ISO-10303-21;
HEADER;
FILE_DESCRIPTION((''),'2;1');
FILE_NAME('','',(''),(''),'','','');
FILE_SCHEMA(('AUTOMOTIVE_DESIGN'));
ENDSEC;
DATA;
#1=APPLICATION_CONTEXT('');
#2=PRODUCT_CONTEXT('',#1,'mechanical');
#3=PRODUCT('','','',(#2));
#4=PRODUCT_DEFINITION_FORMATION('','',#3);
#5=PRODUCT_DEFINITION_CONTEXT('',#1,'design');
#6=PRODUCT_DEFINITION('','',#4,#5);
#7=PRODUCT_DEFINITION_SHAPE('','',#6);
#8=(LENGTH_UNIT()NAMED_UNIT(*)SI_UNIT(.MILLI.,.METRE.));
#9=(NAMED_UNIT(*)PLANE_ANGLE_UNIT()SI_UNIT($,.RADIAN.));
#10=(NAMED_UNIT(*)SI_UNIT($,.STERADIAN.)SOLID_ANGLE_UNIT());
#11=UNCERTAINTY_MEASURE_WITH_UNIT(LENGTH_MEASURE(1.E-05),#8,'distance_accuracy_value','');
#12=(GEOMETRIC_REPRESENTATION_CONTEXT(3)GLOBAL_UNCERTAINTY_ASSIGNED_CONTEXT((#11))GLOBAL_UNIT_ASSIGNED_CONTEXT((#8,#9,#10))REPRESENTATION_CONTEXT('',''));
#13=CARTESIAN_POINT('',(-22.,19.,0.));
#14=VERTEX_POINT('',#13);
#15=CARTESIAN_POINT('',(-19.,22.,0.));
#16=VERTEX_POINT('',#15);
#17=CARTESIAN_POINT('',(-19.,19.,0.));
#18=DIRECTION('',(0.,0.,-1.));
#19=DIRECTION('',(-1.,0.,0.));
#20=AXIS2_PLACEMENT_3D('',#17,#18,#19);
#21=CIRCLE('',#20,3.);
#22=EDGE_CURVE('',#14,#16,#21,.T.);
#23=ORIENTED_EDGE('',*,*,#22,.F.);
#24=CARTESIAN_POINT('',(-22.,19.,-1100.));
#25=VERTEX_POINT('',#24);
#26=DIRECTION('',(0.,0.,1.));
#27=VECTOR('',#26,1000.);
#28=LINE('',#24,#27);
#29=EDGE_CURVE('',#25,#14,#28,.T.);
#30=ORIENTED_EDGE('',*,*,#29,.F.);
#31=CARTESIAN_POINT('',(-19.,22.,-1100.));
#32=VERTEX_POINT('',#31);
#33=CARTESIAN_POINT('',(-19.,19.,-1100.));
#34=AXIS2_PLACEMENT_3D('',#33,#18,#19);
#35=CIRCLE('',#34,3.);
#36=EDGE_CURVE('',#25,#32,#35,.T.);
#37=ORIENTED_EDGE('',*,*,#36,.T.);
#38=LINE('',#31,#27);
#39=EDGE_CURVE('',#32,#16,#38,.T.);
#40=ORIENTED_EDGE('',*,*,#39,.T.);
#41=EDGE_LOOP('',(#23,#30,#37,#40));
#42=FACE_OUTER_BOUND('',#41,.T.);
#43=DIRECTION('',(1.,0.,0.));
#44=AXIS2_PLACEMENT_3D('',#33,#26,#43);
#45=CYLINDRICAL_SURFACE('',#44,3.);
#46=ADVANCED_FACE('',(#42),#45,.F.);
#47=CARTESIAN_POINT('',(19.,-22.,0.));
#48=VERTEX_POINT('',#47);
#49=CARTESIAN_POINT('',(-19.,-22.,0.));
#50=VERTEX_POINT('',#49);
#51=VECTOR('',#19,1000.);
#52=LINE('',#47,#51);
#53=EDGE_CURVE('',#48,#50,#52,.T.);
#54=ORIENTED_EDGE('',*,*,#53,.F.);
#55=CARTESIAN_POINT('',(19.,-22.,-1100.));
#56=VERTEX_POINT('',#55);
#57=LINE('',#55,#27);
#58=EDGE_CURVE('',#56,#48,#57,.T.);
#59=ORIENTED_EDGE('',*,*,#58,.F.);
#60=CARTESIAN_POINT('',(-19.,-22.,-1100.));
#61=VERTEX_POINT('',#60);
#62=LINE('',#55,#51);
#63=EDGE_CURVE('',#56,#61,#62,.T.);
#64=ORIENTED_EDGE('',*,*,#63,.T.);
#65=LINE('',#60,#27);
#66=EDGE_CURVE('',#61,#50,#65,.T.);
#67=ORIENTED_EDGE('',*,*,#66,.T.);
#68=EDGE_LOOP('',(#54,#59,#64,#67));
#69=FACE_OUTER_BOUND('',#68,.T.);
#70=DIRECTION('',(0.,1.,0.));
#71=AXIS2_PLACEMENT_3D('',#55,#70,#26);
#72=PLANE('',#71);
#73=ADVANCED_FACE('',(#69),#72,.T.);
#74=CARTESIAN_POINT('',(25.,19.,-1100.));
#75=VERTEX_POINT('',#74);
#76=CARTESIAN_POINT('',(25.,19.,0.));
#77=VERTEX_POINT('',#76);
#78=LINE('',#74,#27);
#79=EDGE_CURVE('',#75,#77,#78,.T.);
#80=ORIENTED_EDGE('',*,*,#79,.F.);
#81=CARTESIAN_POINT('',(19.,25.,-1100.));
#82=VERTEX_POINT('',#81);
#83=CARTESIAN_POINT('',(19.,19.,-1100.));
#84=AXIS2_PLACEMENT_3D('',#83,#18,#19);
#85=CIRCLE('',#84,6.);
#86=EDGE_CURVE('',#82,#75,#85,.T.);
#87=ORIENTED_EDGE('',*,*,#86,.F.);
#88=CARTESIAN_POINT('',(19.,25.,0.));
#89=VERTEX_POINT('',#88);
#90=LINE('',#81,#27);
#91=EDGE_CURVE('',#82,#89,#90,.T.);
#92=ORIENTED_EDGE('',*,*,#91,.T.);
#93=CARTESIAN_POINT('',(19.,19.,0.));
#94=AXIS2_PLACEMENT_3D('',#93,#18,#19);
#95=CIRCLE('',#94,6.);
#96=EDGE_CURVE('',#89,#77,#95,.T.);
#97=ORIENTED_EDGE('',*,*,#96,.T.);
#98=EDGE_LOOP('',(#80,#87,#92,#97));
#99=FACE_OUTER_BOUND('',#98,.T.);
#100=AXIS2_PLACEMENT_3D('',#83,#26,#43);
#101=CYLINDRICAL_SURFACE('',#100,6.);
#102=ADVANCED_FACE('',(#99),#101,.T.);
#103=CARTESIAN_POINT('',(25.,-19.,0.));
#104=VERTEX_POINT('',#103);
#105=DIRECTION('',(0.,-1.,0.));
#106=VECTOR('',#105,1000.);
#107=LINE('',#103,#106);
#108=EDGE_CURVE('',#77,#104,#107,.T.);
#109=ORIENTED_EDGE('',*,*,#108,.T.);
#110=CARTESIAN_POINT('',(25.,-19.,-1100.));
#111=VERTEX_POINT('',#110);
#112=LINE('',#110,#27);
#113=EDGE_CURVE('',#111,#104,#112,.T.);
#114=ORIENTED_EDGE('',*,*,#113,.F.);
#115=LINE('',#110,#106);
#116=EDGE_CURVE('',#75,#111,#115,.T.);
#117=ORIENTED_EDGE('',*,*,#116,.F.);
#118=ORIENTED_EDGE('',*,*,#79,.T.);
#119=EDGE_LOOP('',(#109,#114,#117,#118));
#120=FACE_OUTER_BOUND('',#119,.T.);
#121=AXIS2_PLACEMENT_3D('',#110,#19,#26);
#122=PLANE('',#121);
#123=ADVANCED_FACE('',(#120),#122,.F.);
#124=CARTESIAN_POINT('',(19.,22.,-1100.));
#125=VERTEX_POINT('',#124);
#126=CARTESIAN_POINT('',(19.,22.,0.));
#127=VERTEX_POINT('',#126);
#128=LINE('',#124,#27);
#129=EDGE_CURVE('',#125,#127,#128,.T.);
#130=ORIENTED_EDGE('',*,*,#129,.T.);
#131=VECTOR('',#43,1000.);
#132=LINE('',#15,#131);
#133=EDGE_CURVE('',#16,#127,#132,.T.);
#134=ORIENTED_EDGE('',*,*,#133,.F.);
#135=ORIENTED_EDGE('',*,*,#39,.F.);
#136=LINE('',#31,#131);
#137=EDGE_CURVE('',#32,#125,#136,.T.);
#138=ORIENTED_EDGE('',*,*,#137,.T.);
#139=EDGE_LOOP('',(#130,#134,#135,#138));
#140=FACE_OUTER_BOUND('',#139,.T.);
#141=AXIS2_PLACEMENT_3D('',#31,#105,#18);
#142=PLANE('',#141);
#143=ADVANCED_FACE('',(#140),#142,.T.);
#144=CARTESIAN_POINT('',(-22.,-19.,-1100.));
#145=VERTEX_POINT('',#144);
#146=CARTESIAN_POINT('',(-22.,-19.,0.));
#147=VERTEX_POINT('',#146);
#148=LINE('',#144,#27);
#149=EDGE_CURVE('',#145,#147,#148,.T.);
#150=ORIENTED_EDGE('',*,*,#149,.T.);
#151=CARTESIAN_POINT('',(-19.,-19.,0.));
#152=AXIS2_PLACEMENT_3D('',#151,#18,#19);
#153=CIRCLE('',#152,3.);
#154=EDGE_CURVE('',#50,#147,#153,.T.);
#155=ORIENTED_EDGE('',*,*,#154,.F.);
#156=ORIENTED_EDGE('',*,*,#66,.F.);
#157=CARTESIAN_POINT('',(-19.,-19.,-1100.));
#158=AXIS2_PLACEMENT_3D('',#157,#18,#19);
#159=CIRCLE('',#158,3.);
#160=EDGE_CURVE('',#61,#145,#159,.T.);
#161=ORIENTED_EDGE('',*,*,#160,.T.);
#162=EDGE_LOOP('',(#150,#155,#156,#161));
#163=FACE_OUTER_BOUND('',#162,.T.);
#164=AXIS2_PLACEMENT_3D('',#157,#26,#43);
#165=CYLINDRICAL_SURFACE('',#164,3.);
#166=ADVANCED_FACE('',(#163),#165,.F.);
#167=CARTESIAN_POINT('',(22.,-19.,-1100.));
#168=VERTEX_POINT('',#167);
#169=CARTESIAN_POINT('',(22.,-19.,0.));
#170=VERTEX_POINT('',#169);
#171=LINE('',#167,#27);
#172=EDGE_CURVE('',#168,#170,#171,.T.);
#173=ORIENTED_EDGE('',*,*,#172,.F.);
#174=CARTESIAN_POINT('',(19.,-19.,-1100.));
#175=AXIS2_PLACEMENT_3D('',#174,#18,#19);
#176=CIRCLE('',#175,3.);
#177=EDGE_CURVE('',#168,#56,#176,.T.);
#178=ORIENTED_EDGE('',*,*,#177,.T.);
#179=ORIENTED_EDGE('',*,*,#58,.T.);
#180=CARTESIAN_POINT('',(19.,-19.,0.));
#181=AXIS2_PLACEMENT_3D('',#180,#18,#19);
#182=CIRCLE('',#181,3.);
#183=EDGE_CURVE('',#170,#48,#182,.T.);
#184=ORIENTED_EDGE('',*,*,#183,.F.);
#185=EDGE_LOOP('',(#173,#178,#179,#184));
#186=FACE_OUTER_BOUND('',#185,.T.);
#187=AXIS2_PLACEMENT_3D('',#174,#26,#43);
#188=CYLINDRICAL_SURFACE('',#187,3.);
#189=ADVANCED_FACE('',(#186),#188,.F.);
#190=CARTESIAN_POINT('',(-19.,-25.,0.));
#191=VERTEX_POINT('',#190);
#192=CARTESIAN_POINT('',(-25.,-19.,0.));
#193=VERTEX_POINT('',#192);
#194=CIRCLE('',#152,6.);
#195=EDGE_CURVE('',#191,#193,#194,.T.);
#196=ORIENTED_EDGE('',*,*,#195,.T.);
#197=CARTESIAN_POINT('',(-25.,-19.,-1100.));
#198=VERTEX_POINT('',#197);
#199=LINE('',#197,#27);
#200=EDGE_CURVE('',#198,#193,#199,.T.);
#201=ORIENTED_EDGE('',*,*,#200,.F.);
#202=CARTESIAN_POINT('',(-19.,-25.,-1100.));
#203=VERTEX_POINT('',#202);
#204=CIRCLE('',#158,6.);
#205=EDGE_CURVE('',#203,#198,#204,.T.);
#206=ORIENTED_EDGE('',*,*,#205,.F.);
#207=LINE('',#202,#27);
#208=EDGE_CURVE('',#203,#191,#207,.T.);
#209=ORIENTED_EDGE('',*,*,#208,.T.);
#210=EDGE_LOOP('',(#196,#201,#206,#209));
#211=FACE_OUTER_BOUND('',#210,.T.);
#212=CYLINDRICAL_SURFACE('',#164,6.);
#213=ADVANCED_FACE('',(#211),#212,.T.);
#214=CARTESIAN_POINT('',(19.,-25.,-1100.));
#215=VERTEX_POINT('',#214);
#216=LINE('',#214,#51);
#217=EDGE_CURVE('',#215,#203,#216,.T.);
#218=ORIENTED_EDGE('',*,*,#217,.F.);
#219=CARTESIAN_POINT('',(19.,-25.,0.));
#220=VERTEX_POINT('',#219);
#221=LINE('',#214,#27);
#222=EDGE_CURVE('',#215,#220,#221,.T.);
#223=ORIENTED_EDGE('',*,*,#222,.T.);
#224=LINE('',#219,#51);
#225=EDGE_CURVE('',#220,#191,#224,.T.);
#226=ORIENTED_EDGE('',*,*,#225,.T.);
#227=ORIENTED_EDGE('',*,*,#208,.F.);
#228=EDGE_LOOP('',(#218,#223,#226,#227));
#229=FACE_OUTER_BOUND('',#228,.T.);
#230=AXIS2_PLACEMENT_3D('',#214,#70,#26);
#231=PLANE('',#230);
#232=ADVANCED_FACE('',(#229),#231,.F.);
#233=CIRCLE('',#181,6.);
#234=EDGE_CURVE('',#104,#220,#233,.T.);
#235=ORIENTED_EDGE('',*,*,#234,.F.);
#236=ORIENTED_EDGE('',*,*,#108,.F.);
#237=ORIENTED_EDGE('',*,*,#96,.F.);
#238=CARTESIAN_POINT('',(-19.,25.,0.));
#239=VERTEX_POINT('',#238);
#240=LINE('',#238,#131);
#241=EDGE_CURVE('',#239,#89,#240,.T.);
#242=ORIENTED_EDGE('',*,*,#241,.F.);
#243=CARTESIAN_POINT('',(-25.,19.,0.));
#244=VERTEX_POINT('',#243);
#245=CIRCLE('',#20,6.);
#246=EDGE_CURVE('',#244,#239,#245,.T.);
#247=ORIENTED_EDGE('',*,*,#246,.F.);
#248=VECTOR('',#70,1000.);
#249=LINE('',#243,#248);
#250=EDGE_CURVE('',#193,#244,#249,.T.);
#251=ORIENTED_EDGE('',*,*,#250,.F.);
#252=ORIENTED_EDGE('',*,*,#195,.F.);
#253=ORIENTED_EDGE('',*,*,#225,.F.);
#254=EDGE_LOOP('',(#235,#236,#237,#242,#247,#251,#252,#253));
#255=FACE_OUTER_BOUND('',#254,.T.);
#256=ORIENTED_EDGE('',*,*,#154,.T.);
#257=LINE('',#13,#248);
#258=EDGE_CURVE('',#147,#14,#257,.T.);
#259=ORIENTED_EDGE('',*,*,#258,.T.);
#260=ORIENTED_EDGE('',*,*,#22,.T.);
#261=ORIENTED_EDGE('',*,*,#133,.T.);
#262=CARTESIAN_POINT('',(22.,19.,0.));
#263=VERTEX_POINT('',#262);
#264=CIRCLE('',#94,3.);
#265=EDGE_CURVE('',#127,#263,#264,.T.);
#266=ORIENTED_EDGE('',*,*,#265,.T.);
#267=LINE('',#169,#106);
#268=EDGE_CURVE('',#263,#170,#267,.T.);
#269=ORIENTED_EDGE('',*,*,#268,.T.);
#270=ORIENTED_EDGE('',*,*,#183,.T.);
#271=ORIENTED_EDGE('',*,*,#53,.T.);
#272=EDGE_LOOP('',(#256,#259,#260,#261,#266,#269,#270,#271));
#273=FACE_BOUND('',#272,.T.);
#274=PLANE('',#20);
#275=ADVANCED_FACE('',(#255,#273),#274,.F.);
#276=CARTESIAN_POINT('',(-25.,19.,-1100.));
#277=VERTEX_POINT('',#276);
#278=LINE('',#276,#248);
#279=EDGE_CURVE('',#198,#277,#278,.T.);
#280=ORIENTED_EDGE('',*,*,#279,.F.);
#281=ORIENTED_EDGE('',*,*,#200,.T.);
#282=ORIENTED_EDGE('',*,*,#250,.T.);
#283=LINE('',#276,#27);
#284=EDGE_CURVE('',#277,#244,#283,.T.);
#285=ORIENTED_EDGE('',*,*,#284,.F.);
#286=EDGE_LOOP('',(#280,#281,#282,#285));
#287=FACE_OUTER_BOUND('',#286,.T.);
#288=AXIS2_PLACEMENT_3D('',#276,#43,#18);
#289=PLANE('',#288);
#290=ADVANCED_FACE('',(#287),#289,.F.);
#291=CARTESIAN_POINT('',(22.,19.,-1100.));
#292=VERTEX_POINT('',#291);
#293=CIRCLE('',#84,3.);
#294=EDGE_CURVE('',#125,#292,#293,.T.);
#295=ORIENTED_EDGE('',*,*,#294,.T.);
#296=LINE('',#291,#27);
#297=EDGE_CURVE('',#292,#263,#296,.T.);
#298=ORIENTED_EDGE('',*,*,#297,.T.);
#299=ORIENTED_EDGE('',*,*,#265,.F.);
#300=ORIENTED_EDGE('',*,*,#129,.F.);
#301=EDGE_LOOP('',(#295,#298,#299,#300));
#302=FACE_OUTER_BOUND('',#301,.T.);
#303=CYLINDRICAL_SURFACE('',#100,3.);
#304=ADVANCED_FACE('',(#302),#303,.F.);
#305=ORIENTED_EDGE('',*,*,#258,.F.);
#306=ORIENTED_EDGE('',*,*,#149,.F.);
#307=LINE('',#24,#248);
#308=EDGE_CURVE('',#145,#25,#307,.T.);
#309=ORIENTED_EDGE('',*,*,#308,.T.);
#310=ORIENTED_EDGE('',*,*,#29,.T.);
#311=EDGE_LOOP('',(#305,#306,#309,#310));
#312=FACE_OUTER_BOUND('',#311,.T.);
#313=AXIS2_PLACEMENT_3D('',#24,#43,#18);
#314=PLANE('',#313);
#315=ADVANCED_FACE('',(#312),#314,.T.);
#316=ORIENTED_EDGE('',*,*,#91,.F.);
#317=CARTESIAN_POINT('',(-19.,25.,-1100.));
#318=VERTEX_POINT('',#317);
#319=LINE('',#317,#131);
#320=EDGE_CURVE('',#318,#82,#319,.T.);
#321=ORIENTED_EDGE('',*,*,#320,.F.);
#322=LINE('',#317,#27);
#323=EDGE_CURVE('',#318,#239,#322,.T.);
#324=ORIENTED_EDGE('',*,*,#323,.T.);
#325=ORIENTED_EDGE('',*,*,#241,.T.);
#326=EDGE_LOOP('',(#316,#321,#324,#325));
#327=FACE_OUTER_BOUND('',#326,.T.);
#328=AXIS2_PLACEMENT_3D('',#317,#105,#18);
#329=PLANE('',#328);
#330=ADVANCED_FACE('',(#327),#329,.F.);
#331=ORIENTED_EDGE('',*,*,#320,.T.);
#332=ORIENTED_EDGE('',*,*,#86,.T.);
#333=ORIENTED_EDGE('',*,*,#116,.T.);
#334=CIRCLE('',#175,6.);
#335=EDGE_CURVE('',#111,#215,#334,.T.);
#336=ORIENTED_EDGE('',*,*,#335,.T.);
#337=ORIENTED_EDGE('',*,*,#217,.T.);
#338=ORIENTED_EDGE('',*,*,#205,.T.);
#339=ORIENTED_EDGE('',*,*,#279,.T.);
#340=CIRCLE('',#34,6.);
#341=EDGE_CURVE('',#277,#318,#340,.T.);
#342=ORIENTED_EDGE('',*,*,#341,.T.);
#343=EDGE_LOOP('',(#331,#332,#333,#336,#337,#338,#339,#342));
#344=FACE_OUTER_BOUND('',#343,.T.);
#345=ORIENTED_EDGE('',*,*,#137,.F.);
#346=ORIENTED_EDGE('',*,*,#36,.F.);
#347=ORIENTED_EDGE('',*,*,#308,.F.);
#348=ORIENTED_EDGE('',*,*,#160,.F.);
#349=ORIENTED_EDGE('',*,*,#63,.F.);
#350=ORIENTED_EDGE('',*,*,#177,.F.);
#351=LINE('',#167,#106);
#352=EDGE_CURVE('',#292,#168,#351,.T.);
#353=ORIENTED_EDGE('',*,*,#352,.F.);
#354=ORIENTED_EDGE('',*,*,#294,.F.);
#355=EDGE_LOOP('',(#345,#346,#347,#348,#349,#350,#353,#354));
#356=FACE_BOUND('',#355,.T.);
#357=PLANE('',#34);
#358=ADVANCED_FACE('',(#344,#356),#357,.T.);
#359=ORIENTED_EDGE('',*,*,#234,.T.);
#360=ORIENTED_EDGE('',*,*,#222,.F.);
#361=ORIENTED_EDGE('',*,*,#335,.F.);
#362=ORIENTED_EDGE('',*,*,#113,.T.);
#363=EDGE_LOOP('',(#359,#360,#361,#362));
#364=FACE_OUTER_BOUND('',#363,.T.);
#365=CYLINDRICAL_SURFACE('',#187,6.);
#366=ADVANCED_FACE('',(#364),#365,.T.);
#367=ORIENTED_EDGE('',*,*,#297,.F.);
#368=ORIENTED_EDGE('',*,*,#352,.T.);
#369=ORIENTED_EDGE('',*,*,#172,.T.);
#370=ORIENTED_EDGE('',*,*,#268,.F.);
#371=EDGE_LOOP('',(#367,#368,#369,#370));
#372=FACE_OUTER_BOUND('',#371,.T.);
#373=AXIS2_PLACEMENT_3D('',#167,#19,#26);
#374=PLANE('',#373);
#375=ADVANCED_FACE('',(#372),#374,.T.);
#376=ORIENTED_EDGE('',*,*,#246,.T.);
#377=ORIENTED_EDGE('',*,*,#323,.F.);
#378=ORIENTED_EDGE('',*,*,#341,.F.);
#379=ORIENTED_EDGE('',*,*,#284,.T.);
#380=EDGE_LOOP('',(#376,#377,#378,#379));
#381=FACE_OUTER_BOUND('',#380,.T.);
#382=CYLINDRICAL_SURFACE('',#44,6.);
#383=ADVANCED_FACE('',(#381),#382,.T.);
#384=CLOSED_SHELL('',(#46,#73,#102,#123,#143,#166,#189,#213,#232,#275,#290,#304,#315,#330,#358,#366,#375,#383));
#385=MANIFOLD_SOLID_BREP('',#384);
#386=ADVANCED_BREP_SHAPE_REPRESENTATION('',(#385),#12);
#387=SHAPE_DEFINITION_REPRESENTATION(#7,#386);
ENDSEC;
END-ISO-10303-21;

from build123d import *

# Parameters (mm, degrees)
GB_6728_1986_050_X_50_X_3_1_DEPTH = 1100


with BuildPart() as part:
    # Sketch1 → Gb／6728-1986方形空心型钢 050 X 50 X 3(1) (new body)
    with BuildSketch(Plane(origin=(0, 0, 0), x_dir=(-1, 0, 0), z_dir=(0, 0, -1))):
        with BuildLine():
            Line((-19, -25), (19, -25))
            ThreePointArc((19, -25), (23.242640687, -23.242640687), (25, -19))
            Line((25, -19), (25, 19))
            ThreePointArc((25, 19), (23.242640687, 23.242640687), (19, 25))
            Line((19, 25), (-19, 25))
            ThreePointArc((-19, 25), (-23.242640687, 23.242640687), (-25, 19))
            Line((-25, 19), (-25, -19))
            ThreePointArc((-25, -19), (-23.242640687, -23.242640687), (-19, -25))
        make_face()
        with BuildLine():
            Line((-19, -22), (19, -22))
            ThreePointArc((19, -22), (21.121320344, -21.121320344), (22, -19))
            Line((22, -19), (22, 19))
            ThreePointArc((22, 19), (21.121320344, 21.121320344), (19, 22))
            Line((19, 22), (-19, 22))
            ThreePointArc((-19, 22), (-21.121320344, 21.121320344), (-22, 19))
            Line((-22, 19), (-22, -19))
            ThreePointArc((-22, -19), (-21.121320344, -21.121320344), (-19, -22))
        make_face(mode=Mode.SUBTRACT)
    extrude(amount=GB_6728_1986_050_X_50_X_3_1_DEPTH)


solid = part.part
